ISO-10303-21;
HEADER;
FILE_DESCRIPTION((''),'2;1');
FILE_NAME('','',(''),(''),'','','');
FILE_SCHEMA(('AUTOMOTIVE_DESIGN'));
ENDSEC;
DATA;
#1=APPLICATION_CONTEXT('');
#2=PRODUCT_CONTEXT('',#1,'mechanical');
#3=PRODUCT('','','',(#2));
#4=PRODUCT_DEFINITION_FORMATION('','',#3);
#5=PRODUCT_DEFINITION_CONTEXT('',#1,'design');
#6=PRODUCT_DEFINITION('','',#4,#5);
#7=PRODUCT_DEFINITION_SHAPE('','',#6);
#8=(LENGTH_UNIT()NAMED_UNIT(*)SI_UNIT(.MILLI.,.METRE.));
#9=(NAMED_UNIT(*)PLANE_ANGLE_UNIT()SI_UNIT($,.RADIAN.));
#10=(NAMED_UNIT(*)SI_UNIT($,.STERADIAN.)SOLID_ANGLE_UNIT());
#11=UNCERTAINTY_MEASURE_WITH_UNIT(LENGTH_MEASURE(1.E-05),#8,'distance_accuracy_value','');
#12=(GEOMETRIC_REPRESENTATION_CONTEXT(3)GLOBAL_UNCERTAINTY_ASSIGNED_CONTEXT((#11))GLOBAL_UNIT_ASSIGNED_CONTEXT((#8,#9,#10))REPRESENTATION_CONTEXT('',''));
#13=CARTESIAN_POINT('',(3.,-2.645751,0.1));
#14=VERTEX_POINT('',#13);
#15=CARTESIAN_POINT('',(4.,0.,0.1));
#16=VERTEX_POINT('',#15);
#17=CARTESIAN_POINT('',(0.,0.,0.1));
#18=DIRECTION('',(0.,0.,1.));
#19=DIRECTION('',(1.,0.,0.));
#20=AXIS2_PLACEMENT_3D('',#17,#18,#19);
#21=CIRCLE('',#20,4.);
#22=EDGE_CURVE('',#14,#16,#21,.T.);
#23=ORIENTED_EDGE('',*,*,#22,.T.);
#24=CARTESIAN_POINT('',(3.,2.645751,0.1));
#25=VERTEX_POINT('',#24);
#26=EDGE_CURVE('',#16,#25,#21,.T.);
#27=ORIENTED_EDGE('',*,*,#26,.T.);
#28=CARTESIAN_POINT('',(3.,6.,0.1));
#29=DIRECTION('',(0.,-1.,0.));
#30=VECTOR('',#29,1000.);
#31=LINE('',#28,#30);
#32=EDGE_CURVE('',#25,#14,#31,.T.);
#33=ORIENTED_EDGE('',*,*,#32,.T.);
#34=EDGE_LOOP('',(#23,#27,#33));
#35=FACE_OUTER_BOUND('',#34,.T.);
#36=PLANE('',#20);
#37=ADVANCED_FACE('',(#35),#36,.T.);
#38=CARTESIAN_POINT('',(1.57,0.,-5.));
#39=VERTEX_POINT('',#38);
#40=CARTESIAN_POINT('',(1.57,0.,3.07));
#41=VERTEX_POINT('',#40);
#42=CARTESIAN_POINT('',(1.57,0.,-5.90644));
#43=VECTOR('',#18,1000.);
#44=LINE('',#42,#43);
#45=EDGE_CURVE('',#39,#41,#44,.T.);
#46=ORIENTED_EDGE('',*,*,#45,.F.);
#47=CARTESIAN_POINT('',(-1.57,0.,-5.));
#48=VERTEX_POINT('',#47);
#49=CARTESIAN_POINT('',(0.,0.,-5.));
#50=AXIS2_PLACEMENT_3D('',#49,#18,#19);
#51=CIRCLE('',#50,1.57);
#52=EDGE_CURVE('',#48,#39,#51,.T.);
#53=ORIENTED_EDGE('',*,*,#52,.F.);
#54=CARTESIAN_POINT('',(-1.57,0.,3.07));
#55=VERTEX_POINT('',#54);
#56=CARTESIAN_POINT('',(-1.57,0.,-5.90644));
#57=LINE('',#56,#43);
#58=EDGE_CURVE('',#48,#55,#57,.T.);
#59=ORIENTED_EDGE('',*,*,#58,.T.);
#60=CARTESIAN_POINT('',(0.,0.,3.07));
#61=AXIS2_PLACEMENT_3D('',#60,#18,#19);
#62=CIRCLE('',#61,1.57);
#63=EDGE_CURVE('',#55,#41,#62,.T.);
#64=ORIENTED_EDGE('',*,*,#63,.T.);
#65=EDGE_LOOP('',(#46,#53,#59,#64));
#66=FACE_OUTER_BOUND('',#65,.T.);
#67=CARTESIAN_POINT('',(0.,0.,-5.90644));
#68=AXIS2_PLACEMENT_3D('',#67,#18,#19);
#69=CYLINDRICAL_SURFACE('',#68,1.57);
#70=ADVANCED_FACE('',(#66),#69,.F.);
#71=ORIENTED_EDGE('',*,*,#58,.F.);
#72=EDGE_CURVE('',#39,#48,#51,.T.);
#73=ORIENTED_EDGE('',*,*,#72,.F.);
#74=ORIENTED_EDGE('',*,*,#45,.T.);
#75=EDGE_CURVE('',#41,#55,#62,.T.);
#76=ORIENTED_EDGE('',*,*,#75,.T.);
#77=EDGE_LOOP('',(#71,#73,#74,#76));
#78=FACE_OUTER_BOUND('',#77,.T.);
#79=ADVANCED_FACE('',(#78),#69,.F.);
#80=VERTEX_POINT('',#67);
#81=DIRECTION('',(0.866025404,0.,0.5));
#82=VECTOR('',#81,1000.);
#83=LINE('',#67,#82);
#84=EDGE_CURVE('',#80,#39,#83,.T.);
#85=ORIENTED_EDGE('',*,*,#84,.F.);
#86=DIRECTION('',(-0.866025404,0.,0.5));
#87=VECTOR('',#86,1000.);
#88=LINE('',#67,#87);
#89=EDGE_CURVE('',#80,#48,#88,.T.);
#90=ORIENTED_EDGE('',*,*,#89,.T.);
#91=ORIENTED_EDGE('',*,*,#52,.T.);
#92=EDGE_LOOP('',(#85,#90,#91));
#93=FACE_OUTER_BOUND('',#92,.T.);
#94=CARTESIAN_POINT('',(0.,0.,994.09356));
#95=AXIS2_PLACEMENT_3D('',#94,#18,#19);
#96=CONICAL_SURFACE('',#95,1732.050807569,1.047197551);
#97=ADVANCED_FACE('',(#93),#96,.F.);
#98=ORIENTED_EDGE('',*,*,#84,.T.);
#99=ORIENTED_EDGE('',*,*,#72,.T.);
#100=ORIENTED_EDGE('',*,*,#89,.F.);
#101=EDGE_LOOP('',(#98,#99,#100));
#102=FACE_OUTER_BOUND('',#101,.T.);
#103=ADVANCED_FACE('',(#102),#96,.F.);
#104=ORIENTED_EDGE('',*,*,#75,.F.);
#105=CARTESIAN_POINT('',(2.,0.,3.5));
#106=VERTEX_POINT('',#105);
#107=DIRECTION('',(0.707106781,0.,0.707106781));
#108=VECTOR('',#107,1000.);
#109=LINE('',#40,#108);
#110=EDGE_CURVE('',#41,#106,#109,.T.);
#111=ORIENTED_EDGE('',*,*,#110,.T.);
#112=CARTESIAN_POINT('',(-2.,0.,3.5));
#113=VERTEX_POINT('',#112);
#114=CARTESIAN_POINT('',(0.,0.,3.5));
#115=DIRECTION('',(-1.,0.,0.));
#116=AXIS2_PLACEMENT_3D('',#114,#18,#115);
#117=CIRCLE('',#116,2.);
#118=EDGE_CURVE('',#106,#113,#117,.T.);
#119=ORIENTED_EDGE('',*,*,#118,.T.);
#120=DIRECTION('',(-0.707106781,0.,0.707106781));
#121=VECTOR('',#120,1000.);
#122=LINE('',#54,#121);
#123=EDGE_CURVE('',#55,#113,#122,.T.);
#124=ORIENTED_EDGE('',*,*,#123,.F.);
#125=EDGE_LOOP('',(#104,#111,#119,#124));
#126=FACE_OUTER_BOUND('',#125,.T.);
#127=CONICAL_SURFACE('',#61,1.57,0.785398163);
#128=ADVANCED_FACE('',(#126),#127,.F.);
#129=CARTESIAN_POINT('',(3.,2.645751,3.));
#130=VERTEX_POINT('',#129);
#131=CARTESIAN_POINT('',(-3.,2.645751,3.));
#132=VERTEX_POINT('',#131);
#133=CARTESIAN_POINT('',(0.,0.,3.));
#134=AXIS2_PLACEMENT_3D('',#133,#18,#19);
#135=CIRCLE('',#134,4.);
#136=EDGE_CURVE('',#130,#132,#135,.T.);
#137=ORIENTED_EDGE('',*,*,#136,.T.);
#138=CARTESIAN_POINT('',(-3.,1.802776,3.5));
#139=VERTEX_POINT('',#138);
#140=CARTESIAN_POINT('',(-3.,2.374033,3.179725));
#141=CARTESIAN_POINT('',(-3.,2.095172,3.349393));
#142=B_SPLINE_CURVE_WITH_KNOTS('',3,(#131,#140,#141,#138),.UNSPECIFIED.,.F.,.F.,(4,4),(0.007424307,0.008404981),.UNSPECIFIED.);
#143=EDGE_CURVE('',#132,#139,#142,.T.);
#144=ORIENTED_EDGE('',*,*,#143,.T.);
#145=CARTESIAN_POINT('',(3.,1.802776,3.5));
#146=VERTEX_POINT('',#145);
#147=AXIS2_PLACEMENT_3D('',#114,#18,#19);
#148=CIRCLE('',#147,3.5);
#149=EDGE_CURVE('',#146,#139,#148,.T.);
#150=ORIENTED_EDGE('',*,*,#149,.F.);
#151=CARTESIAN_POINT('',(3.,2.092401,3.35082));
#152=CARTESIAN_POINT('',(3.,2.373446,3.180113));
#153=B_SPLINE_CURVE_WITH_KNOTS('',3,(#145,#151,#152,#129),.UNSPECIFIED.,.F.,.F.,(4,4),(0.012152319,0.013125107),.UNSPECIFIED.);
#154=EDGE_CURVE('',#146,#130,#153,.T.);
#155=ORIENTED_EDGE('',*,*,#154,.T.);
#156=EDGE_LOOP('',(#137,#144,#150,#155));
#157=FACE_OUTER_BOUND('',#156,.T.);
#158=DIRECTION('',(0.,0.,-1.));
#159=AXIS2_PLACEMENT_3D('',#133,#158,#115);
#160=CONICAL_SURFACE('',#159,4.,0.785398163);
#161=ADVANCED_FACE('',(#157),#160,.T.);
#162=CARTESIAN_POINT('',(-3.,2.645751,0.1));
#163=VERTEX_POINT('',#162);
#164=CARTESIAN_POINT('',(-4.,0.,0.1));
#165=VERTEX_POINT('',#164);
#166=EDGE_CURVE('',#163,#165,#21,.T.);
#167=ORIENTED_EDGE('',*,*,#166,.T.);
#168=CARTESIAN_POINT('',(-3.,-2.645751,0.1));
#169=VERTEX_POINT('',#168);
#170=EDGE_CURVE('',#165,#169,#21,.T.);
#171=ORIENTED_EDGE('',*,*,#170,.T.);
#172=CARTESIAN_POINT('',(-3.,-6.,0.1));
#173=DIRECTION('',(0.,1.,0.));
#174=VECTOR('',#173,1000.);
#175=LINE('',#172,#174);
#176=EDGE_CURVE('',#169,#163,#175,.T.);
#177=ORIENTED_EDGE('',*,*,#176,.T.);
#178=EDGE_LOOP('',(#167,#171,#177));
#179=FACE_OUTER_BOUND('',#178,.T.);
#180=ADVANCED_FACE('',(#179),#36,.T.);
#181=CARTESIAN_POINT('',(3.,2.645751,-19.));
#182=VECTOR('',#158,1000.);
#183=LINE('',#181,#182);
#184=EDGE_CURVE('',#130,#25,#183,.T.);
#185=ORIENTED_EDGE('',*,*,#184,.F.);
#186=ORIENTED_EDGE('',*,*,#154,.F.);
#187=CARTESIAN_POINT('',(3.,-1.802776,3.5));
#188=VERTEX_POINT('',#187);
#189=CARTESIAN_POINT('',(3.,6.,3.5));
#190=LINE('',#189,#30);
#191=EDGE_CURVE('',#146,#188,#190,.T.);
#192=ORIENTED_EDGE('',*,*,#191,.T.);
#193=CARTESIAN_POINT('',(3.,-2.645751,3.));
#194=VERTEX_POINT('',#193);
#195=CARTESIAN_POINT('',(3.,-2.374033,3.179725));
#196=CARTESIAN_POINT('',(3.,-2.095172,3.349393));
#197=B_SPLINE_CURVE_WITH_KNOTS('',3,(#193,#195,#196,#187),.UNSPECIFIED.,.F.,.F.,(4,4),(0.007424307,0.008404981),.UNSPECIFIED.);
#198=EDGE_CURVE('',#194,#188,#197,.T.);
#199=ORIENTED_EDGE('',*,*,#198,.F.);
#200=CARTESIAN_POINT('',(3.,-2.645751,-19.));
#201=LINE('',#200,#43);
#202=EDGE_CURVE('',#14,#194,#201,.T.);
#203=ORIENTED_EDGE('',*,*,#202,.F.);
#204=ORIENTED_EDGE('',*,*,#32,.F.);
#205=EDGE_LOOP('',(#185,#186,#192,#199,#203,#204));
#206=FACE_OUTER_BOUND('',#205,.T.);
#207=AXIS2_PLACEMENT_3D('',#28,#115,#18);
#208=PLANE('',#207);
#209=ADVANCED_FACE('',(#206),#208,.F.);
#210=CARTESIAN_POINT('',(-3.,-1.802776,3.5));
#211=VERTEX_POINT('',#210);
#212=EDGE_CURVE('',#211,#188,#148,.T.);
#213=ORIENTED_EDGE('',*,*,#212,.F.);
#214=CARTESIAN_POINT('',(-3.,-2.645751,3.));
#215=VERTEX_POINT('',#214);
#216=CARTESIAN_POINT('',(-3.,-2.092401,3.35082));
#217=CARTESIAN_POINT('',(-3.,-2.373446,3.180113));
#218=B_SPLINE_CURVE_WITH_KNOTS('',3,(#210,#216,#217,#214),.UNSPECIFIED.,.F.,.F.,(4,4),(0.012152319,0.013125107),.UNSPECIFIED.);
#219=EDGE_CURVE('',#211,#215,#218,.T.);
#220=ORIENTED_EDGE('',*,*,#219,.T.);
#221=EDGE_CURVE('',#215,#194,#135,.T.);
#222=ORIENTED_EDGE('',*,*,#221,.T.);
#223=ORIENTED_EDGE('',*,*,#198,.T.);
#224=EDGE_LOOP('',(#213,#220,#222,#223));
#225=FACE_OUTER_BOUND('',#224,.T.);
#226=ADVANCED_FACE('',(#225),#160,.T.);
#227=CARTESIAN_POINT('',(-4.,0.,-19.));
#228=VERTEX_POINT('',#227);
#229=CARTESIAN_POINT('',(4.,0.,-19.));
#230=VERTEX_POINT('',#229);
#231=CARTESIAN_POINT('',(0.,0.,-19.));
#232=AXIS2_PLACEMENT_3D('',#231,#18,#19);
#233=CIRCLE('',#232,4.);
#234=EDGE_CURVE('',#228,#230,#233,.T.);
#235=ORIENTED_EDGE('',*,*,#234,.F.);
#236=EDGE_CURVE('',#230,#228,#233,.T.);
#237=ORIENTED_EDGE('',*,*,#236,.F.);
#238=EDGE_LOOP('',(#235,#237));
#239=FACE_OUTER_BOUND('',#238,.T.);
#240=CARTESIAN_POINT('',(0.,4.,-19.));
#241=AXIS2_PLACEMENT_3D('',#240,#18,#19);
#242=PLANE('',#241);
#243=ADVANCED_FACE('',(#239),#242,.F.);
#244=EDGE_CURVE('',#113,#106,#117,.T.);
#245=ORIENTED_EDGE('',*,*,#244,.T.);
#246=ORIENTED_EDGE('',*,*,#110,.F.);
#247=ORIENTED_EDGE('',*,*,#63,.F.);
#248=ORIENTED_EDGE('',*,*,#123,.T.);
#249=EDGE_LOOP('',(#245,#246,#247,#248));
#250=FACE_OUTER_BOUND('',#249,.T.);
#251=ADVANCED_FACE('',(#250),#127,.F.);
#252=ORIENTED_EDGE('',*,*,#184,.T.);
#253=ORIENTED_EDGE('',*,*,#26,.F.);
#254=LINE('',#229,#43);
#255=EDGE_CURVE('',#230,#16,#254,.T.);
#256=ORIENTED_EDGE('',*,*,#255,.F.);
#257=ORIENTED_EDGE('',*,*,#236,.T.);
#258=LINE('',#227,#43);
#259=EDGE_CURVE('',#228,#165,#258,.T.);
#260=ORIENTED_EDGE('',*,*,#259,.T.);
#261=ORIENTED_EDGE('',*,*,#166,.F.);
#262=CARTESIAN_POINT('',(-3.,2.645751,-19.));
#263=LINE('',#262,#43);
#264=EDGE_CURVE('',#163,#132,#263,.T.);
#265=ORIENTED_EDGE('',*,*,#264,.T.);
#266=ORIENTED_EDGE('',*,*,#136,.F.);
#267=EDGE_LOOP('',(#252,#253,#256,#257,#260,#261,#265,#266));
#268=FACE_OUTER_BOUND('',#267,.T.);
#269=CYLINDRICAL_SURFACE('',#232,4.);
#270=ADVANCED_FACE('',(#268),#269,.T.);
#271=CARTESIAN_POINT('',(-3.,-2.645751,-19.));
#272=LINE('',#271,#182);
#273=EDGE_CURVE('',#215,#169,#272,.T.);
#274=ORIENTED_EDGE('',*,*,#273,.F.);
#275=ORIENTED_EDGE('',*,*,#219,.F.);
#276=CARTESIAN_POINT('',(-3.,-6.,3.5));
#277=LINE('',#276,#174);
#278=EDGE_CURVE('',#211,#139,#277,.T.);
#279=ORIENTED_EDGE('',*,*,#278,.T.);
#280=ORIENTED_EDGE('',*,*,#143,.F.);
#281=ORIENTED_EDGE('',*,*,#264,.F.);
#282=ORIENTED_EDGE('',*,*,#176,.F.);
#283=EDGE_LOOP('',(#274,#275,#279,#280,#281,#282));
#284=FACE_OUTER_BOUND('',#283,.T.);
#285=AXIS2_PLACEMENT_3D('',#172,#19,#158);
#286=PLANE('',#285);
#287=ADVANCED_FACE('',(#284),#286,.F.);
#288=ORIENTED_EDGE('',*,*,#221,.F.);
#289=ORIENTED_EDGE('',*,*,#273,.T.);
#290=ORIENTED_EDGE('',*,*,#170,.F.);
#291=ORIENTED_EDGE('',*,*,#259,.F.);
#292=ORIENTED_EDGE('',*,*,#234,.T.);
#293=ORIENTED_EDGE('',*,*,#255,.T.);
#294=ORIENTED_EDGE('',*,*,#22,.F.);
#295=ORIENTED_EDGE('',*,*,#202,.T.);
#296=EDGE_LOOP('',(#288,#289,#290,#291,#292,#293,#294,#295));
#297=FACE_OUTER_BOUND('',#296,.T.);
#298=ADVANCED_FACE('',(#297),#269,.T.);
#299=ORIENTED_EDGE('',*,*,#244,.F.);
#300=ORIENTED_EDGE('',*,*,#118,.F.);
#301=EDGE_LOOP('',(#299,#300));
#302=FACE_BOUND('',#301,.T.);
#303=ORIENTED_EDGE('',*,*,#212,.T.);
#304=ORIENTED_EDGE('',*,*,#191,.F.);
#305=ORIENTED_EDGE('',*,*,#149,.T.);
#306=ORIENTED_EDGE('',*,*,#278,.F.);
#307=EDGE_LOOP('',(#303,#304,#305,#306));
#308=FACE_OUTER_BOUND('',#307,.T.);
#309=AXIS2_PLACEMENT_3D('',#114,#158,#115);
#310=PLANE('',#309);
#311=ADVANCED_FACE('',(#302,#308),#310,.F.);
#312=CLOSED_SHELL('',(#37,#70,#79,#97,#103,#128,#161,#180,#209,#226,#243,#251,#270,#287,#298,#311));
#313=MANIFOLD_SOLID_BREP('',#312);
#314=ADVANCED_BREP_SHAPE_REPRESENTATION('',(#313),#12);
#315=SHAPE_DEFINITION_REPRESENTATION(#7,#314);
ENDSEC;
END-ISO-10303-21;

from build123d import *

# Parameters (mm, degrees)
CUT_EXTRUDE_1_DEPTH = 3.4


with BuildPart() as part:
    # 草图1 → 旋转1 (revolve)
    with BuildSketch(Plane(origin=(0, 0, 0), x_dir=(0, 0, -1), z_dir=(1, 0, 0)), mode=Mode.PRIVATE) as revolve_1_sk:
        Polygon((-3.5, 0), (-3.5, 3.5), (-3, 4), (19, 4), (19, 0), align=None)
    revolve(revolve_1_sk.sketch.rotate(Axis((0, 0, -19), (0, 0, 1)), 270), axis=Axis((0, 0, -19), (0, 0, 1)))

    # 草图2 → 切除-拉伸1 (cut)
    with BuildSketch(Plane.XY.offset(3.5)):
        Polygon((-6, -6), (-3, -6), (-3, 6), (3, 6), (3, -6), (6, -6), (6, 8), (-6, 8), align=None)
    extrude(amount=-CUT_EXTRUDE_1_DEPTH, mode=Mode.SUBTRACT)

    # 草图3 → 切除-旋转1 (revolve, cut)
    with BuildSketch(Plane(origin=(0, 0, 0), x_dir=(0, 0, -1), z_dir=(1, 0, 0)), mode=Mode.PRIVATE) as cut_revolve_1_sk:
        Polygon((-4, 0), (-4, 2.5), (-3.07, 1.57), (5, 1.57), (5.906439923, 0), align=None)
    revolve(cut_revolve_1_sk.sketch.rotate(Axis((0, 0, -5.906439923), (0, 0, 1)), 270), axis=Axis((0, 0, -5.906439923), (0, 0, 1)), mode=Mode.SUBTRACT)


solid = part.part
